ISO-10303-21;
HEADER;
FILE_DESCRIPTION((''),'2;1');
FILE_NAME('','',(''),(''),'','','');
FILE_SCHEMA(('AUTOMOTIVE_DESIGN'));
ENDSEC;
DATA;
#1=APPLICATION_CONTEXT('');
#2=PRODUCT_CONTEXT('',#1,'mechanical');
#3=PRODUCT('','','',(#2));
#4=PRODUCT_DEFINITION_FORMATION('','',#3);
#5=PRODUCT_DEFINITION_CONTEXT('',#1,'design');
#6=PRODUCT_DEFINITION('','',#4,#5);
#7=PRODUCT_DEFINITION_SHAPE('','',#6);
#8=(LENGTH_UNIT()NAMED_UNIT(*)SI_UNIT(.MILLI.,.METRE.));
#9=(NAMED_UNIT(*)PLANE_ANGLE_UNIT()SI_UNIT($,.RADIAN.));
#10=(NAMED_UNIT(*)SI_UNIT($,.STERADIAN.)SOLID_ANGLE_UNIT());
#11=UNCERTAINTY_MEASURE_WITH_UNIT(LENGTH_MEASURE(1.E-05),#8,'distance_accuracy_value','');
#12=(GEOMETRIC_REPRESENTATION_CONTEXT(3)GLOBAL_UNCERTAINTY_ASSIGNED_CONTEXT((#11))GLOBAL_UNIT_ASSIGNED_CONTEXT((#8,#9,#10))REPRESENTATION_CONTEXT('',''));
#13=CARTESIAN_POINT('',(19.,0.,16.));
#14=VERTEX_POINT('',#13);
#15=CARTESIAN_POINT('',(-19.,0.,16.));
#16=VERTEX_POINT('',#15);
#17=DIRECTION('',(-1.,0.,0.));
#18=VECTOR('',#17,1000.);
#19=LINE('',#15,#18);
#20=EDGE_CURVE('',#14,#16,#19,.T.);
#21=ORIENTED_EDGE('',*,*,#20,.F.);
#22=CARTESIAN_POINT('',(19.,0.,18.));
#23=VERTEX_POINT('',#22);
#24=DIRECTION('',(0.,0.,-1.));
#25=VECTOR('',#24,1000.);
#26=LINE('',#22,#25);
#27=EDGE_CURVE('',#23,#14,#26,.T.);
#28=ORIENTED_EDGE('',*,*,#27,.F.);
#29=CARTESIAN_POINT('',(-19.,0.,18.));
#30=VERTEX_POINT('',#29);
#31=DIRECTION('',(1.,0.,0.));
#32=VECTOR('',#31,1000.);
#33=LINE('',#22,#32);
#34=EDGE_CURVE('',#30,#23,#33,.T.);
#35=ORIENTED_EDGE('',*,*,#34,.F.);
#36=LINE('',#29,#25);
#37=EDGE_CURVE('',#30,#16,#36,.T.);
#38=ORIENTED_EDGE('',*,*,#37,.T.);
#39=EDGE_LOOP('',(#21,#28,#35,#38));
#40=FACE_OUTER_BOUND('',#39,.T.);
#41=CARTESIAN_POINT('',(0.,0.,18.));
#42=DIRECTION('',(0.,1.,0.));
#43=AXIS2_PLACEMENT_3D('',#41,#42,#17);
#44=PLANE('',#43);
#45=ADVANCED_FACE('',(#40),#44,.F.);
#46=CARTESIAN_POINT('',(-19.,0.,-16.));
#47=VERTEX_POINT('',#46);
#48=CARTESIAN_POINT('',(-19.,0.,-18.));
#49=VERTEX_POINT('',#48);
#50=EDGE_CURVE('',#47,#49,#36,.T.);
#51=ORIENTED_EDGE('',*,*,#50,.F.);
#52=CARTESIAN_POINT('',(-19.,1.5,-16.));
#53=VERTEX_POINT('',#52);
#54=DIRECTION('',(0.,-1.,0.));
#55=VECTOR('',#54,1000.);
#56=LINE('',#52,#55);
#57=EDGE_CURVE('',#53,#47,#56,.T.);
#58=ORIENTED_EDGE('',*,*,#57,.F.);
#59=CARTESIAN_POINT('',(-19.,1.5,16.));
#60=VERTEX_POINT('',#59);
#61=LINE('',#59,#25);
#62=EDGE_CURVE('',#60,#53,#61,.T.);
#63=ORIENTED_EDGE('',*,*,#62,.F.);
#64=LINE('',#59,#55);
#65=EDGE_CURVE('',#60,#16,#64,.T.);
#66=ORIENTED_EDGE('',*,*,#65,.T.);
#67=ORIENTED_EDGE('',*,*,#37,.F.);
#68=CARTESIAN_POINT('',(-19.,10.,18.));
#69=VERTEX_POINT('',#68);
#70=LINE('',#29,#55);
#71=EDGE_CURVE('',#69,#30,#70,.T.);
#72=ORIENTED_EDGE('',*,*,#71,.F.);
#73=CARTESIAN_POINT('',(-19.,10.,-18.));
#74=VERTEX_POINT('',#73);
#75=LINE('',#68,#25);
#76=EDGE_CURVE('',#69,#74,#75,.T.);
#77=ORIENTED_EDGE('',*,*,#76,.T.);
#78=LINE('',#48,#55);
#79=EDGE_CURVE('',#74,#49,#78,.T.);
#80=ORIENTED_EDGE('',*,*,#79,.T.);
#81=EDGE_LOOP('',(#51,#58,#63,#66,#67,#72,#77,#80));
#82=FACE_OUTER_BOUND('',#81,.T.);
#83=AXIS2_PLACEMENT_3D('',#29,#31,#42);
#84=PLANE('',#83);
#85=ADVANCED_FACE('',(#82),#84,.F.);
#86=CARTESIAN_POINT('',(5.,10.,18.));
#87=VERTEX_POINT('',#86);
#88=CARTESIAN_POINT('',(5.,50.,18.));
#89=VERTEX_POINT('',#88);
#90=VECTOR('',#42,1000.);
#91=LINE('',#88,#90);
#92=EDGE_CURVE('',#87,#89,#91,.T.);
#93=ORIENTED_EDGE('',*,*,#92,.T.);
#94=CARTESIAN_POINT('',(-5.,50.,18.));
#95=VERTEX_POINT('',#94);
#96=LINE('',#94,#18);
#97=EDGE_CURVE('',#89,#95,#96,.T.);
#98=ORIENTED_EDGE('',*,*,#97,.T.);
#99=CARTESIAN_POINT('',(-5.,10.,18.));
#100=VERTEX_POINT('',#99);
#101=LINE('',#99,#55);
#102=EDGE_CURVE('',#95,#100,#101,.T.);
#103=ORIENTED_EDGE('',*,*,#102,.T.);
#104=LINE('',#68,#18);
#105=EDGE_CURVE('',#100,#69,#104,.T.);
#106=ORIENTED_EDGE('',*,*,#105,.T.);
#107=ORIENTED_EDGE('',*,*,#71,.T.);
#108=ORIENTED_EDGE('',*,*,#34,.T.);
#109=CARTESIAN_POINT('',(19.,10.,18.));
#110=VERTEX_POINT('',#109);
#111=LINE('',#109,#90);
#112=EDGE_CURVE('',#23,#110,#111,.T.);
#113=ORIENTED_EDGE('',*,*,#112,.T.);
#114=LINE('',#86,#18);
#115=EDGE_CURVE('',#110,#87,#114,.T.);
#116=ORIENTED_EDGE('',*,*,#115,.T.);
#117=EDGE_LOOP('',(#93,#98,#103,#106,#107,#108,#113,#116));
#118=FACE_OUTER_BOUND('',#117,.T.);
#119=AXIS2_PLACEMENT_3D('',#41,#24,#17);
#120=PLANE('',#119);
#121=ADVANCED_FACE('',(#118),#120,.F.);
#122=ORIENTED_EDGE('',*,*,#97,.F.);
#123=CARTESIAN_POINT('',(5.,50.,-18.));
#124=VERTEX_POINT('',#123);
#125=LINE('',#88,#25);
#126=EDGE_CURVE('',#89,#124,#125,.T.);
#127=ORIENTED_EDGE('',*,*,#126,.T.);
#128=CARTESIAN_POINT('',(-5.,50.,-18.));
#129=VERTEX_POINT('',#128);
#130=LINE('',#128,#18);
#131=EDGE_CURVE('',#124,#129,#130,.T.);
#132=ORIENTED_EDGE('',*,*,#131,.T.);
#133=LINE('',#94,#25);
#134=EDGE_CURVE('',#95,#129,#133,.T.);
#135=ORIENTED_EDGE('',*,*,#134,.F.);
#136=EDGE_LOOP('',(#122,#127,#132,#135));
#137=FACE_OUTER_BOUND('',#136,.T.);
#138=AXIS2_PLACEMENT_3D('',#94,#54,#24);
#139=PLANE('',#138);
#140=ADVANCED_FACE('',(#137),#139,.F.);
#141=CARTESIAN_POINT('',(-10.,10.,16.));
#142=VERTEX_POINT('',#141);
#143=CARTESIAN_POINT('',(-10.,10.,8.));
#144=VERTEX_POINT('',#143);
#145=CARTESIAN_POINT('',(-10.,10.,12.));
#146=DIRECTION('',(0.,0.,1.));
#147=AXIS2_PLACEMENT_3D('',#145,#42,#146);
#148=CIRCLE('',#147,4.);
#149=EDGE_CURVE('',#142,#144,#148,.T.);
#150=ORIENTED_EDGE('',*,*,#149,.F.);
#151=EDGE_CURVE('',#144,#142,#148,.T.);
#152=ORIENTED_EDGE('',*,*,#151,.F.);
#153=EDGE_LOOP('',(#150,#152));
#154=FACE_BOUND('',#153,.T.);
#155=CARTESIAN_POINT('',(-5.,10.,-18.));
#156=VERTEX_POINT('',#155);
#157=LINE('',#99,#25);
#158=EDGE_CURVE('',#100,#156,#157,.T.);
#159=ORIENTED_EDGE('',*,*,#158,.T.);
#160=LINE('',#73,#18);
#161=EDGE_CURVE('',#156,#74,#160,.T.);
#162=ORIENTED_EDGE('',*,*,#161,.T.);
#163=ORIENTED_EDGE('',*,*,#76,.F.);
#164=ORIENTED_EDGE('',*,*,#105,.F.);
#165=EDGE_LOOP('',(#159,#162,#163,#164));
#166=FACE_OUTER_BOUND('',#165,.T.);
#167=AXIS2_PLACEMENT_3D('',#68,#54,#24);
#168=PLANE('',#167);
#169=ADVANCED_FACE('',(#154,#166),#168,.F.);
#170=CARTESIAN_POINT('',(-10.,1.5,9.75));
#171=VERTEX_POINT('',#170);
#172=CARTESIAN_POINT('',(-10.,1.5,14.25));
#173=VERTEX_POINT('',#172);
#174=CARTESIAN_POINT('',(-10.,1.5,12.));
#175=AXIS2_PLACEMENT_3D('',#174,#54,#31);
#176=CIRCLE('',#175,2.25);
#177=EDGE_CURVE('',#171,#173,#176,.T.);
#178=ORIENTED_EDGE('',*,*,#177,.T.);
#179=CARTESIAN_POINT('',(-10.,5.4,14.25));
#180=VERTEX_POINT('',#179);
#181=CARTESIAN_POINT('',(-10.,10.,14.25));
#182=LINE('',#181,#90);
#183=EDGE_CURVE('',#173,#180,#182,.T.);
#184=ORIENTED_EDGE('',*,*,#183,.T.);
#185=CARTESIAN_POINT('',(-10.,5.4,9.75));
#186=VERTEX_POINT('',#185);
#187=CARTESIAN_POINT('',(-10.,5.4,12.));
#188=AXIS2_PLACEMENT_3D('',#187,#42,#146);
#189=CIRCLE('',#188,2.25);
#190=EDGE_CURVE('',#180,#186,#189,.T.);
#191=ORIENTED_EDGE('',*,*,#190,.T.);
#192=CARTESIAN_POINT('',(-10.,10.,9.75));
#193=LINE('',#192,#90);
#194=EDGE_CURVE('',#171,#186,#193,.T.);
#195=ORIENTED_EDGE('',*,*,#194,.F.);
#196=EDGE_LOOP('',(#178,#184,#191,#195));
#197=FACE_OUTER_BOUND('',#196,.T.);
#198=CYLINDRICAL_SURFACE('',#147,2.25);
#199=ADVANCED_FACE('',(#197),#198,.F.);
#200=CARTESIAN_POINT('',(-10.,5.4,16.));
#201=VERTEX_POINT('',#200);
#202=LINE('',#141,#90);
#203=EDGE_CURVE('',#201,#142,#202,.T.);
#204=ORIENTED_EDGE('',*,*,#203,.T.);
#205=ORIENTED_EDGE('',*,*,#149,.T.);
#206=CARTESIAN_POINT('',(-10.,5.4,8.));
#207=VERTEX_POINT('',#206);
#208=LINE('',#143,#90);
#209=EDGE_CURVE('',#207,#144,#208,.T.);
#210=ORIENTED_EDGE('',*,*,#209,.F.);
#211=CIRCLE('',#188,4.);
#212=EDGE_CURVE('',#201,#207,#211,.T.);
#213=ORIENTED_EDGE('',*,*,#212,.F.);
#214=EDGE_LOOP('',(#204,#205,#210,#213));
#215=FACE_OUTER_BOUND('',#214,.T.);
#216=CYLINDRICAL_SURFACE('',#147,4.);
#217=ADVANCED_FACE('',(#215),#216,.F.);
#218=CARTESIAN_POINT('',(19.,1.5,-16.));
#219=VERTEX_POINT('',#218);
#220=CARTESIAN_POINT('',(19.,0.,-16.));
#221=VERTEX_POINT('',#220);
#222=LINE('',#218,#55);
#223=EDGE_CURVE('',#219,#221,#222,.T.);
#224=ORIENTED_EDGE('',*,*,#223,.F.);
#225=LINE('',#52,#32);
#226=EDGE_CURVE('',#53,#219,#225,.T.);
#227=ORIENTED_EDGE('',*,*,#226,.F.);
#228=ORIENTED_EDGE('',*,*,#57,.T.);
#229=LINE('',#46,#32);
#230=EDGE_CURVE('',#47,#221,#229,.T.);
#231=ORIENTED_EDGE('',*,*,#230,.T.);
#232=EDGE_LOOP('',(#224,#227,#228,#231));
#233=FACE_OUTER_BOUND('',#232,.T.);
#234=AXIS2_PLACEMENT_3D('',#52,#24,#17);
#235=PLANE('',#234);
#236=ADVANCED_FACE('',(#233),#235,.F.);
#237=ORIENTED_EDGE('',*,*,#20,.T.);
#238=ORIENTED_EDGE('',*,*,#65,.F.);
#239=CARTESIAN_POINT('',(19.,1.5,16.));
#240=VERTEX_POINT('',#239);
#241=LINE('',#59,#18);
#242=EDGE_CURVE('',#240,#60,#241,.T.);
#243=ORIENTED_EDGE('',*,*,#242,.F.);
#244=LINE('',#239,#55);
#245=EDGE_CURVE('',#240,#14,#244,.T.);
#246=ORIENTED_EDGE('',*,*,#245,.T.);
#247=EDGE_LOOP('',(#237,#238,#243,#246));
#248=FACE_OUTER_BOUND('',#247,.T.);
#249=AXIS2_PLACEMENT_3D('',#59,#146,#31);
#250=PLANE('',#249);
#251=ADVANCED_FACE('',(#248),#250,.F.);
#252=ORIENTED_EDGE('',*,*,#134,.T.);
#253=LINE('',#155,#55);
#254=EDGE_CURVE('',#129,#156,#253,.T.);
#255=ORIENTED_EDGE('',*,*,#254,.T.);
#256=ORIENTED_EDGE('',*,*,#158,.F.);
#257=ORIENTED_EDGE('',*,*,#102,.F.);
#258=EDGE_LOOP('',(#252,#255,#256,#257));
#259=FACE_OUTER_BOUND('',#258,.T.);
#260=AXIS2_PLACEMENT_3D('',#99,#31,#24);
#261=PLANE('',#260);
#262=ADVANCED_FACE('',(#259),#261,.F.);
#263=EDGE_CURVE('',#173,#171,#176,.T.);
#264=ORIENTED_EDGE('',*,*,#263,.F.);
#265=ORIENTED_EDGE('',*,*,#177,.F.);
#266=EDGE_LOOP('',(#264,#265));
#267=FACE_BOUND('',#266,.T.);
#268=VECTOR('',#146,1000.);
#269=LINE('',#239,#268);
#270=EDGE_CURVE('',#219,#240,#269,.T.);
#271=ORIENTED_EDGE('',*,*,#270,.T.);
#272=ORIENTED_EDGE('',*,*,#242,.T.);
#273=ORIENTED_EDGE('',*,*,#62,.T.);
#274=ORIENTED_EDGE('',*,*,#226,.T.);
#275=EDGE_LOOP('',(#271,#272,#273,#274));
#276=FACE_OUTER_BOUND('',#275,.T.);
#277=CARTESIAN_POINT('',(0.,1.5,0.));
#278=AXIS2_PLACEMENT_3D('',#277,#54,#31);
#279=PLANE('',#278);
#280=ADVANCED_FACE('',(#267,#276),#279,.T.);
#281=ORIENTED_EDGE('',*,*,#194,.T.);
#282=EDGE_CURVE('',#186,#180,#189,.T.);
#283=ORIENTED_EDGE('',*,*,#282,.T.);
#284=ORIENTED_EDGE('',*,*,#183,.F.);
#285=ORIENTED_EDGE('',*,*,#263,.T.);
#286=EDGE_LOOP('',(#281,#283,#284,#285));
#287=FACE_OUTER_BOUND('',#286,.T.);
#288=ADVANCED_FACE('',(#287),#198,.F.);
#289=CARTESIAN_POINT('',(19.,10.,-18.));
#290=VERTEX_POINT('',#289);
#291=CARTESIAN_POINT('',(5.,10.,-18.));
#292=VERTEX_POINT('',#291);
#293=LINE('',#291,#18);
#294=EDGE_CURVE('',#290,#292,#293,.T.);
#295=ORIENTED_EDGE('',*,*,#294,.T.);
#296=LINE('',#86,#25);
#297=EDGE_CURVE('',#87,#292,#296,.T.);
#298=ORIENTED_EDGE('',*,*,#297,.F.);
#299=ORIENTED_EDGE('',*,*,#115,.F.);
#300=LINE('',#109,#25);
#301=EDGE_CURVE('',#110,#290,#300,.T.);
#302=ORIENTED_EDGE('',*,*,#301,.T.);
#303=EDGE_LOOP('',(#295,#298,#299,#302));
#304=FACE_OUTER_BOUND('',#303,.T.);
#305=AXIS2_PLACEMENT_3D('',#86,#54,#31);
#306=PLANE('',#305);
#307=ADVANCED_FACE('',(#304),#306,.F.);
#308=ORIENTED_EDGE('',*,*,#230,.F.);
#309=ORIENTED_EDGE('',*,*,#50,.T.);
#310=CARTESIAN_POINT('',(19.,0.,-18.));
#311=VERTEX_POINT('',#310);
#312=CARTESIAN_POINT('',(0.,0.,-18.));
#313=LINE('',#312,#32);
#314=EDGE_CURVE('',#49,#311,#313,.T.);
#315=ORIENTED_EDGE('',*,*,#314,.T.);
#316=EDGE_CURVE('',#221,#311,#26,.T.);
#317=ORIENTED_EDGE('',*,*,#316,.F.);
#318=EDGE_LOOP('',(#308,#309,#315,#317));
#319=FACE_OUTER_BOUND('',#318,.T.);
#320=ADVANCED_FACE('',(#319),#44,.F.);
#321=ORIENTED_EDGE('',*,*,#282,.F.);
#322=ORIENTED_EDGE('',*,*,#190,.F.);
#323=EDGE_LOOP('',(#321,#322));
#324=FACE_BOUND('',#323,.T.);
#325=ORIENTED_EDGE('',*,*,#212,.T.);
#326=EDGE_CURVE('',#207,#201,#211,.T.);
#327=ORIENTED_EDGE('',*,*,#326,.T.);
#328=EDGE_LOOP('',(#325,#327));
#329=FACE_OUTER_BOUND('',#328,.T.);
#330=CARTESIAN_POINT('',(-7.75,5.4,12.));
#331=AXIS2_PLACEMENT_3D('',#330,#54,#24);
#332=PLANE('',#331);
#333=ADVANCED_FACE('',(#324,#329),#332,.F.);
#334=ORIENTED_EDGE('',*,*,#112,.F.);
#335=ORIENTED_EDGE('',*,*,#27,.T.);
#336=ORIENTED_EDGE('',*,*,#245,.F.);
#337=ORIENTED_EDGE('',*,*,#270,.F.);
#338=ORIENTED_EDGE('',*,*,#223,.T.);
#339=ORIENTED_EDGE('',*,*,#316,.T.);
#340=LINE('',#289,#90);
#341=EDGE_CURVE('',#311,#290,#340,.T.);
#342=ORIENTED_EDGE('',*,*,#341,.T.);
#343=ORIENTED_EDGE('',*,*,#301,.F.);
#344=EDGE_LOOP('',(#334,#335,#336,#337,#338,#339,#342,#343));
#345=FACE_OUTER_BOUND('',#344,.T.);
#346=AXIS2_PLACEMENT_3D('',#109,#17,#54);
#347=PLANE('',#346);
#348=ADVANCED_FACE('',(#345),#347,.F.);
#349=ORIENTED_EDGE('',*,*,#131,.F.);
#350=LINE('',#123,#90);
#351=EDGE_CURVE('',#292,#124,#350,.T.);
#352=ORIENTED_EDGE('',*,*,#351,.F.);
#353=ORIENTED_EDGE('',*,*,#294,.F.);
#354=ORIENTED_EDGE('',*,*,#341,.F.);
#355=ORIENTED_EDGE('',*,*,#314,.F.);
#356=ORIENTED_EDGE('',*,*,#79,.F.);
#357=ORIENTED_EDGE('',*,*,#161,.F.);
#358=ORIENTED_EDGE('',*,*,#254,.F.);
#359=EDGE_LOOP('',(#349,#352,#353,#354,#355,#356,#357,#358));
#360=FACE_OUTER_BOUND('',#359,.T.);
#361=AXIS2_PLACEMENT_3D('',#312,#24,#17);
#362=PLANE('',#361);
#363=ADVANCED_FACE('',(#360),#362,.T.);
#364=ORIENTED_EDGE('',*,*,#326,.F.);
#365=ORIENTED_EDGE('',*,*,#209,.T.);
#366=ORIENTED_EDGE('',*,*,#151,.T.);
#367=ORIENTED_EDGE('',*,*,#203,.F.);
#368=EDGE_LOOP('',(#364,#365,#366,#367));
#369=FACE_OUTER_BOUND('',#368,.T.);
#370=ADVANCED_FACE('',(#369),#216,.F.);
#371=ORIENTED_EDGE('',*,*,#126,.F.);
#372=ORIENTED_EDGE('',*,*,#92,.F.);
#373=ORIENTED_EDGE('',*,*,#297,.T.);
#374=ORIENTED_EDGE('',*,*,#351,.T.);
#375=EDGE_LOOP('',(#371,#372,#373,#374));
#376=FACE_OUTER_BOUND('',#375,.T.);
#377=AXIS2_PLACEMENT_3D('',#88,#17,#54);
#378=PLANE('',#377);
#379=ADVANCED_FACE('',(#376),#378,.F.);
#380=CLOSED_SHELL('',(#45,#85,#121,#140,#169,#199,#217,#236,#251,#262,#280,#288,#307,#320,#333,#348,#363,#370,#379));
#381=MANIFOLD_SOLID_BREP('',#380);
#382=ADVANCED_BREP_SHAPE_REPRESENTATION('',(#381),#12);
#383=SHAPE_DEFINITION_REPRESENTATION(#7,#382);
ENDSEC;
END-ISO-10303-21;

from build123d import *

# Parameters (mm, degrees)
EXTRUDE_1_DEPTH           = 18
SKETCH_2_W                = 38
SKETCH_2_H                = 32
CUT_EXTRUDE_1_DEPTH       = 1.5
HOLE_WIZARD_1_D           = 4.5
HOLE_WIZARD_1_CBORE_D     = 8
HOLE_WIZARD_1_CBORE_DEPTH = 4.6


with BuildPart() as part:
    # 草图1 → 凸台-拉伸1 (new, symmetric)
    with BuildSketch(Plane.XY):
        Polygon((0, 0), (-19, 0), (-19, 10), (-5, 10), (-5, 50), (5, 50), (5, 10), (19, 10), (19, 0), align=None)
    extrude(amount=EXTRUDE_1_DEPTH, both=True)

    # 草图2 → 切除-拉伸1 (cut)
    with BuildSketch(Plane.XZ):
        Rectangle(SKETCH_2_W, SKETCH_2_H)
    extrude(amount=-CUT_EXTRUDE_1_DEPTH, mode=Mode.SUBTRACT)

    # 打孔尺寸(%根据)内六角圆柱头螺钉的类型1 (through all)
    with Locations(Plane(origin=(-10, 10, 12), x_dir=(0, 0, 1), z_dir=(0, 1, 0))):
        with Locations((0, 0)):
            CounterBoreHole(HOLE_WIZARD_1_D / 2, HOLE_WIZARD_1_CBORE_D / 2, HOLE_WIZARD_1_CBORE_DEPTH)


solid = part.part
